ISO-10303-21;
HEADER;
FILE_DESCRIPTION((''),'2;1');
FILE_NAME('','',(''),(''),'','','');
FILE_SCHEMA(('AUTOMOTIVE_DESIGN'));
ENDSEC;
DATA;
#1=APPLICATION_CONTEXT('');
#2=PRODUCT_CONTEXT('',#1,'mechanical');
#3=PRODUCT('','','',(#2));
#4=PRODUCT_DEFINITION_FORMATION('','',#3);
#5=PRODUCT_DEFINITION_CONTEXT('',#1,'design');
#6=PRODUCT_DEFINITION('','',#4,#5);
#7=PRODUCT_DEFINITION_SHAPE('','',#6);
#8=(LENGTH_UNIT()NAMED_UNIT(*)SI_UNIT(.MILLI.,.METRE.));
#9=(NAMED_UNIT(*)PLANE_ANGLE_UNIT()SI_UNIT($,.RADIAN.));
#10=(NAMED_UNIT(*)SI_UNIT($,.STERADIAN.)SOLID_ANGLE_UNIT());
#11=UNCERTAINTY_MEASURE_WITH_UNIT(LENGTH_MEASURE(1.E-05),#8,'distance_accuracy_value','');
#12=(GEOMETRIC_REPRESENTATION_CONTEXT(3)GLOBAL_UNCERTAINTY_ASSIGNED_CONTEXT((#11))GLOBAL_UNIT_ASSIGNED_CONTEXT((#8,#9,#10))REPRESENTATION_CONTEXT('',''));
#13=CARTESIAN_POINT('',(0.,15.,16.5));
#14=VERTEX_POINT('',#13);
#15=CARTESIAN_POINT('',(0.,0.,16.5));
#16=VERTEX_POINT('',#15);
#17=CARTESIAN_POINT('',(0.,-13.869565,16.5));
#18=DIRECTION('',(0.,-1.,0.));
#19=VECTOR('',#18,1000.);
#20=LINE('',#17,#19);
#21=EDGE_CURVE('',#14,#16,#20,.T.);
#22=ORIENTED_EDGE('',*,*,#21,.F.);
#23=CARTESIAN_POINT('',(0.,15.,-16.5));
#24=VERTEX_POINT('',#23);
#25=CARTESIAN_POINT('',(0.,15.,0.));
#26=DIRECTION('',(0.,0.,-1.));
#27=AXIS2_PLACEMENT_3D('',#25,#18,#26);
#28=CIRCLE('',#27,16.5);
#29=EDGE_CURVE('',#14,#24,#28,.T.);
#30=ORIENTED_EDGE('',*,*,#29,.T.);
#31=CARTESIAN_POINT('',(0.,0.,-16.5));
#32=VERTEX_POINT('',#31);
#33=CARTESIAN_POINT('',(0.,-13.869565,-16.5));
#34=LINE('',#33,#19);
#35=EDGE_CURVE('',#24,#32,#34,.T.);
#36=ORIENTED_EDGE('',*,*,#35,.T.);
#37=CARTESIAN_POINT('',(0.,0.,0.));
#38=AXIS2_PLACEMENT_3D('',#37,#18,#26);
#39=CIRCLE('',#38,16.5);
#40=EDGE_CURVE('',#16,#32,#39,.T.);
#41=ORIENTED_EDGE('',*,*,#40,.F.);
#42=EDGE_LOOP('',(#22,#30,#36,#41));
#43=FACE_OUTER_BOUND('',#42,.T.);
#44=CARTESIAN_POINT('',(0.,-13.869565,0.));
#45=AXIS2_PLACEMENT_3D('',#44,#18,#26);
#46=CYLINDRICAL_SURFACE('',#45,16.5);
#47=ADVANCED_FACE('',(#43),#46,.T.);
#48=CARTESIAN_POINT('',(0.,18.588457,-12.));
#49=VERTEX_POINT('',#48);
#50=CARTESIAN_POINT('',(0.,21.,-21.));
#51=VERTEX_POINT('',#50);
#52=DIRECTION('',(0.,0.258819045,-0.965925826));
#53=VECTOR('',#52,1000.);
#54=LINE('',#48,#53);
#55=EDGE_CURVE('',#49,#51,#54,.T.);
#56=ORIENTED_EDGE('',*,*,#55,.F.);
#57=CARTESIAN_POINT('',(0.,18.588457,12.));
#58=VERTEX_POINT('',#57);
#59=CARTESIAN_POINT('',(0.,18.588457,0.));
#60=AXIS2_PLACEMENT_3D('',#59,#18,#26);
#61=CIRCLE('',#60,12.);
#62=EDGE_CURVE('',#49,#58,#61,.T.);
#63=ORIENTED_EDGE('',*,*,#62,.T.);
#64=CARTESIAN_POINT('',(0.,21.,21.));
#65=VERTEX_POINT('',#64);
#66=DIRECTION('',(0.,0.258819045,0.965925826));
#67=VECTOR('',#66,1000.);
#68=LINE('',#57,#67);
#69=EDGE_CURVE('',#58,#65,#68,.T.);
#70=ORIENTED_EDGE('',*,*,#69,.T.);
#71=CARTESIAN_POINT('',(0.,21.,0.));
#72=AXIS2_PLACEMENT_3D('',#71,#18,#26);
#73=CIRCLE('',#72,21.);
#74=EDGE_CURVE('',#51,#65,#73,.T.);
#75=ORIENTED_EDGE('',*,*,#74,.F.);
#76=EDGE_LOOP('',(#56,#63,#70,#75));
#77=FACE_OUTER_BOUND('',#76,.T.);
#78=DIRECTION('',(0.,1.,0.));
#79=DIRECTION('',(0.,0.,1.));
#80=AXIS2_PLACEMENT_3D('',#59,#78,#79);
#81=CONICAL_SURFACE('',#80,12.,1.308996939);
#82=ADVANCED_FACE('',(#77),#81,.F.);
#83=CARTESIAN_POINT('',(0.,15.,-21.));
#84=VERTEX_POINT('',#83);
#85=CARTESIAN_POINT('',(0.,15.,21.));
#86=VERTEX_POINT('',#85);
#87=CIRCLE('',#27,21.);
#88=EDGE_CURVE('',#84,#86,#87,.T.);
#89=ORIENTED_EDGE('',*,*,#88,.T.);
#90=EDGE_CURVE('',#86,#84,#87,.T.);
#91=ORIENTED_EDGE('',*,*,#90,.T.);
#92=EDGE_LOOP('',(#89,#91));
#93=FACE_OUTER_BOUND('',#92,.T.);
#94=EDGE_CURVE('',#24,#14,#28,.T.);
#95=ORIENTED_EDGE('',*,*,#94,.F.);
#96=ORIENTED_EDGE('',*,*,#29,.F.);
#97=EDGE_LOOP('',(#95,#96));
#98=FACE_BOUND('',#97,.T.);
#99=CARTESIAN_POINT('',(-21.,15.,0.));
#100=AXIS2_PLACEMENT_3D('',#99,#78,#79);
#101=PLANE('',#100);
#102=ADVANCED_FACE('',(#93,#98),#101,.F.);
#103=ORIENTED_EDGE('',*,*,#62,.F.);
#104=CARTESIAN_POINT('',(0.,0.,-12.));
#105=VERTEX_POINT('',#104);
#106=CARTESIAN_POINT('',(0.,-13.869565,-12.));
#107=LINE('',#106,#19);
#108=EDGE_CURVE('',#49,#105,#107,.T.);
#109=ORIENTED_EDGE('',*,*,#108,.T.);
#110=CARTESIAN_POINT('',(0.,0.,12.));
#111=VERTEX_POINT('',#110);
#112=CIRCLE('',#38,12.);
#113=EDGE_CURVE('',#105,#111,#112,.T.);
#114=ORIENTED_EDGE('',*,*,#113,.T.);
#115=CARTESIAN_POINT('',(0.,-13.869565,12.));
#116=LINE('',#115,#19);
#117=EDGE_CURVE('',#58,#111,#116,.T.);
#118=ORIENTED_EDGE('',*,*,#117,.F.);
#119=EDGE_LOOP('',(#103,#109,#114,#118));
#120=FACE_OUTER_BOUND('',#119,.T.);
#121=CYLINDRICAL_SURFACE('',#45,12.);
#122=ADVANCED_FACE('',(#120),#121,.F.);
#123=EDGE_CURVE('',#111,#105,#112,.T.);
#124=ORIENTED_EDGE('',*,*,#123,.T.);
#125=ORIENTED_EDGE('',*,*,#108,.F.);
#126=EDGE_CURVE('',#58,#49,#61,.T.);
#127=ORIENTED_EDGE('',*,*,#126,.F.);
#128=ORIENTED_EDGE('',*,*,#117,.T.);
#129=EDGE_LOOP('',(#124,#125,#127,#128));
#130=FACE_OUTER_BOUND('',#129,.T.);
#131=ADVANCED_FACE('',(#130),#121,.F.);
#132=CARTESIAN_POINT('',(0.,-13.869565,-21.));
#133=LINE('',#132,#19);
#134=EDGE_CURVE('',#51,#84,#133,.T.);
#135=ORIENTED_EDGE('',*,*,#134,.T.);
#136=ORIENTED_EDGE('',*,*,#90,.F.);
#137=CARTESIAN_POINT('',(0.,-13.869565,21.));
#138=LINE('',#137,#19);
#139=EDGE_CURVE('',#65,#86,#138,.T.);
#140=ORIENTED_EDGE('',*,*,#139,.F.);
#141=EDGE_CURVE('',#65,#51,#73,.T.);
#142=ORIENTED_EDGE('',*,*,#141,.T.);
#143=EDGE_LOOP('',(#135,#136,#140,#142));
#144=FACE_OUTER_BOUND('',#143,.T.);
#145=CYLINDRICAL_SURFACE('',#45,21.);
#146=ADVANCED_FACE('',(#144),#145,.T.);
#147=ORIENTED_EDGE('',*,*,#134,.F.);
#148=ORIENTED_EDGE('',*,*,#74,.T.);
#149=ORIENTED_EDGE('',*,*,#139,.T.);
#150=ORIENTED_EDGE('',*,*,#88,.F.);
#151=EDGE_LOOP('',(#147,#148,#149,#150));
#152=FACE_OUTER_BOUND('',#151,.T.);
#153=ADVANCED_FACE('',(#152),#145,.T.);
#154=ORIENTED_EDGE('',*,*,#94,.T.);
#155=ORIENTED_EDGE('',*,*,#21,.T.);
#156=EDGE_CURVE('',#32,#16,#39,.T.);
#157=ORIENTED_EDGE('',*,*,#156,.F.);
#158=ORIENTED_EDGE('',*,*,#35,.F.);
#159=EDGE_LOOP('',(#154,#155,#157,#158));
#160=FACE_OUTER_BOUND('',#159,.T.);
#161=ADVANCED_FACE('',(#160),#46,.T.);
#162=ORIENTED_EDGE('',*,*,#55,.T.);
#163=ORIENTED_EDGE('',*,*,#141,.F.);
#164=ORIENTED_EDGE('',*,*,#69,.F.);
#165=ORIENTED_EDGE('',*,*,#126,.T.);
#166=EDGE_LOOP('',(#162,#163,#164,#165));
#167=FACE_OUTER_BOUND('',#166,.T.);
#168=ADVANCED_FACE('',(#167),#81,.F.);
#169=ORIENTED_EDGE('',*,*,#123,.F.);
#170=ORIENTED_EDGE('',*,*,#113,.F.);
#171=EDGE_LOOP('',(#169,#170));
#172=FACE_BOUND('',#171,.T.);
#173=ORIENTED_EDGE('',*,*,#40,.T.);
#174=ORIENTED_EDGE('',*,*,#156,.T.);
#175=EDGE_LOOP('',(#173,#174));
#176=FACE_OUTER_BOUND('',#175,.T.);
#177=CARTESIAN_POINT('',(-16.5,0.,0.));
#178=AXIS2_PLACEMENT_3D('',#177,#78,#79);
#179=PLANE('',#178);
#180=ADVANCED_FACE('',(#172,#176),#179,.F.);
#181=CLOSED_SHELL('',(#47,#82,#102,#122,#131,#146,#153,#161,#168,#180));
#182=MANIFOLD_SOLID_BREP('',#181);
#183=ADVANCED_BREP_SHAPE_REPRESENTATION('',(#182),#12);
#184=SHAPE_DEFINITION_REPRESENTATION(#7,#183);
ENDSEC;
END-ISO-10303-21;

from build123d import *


with BuildPart() as part:
    # Bush Profile Sketch → Flanged Bush Revolve (revolve)
    with BuildSketch(Plane.XY, mode=Mode.PRIVATE) as flanged_bush_revolve_sk:
        Polygon((-12, 0), (-12, 18.588457268), (-21, 21), (-21, 15), (-16.5, 15), (-16.5, 0), align=None)
    revolve(flanged_bush_revolve_sk.sketch.rotate(Axis((0, -13.869565217, 0), (0, 1, 0)), 270), axis=Axis((0, -13.869565217, 0), (0, 1, 0)))


solid = part.part
